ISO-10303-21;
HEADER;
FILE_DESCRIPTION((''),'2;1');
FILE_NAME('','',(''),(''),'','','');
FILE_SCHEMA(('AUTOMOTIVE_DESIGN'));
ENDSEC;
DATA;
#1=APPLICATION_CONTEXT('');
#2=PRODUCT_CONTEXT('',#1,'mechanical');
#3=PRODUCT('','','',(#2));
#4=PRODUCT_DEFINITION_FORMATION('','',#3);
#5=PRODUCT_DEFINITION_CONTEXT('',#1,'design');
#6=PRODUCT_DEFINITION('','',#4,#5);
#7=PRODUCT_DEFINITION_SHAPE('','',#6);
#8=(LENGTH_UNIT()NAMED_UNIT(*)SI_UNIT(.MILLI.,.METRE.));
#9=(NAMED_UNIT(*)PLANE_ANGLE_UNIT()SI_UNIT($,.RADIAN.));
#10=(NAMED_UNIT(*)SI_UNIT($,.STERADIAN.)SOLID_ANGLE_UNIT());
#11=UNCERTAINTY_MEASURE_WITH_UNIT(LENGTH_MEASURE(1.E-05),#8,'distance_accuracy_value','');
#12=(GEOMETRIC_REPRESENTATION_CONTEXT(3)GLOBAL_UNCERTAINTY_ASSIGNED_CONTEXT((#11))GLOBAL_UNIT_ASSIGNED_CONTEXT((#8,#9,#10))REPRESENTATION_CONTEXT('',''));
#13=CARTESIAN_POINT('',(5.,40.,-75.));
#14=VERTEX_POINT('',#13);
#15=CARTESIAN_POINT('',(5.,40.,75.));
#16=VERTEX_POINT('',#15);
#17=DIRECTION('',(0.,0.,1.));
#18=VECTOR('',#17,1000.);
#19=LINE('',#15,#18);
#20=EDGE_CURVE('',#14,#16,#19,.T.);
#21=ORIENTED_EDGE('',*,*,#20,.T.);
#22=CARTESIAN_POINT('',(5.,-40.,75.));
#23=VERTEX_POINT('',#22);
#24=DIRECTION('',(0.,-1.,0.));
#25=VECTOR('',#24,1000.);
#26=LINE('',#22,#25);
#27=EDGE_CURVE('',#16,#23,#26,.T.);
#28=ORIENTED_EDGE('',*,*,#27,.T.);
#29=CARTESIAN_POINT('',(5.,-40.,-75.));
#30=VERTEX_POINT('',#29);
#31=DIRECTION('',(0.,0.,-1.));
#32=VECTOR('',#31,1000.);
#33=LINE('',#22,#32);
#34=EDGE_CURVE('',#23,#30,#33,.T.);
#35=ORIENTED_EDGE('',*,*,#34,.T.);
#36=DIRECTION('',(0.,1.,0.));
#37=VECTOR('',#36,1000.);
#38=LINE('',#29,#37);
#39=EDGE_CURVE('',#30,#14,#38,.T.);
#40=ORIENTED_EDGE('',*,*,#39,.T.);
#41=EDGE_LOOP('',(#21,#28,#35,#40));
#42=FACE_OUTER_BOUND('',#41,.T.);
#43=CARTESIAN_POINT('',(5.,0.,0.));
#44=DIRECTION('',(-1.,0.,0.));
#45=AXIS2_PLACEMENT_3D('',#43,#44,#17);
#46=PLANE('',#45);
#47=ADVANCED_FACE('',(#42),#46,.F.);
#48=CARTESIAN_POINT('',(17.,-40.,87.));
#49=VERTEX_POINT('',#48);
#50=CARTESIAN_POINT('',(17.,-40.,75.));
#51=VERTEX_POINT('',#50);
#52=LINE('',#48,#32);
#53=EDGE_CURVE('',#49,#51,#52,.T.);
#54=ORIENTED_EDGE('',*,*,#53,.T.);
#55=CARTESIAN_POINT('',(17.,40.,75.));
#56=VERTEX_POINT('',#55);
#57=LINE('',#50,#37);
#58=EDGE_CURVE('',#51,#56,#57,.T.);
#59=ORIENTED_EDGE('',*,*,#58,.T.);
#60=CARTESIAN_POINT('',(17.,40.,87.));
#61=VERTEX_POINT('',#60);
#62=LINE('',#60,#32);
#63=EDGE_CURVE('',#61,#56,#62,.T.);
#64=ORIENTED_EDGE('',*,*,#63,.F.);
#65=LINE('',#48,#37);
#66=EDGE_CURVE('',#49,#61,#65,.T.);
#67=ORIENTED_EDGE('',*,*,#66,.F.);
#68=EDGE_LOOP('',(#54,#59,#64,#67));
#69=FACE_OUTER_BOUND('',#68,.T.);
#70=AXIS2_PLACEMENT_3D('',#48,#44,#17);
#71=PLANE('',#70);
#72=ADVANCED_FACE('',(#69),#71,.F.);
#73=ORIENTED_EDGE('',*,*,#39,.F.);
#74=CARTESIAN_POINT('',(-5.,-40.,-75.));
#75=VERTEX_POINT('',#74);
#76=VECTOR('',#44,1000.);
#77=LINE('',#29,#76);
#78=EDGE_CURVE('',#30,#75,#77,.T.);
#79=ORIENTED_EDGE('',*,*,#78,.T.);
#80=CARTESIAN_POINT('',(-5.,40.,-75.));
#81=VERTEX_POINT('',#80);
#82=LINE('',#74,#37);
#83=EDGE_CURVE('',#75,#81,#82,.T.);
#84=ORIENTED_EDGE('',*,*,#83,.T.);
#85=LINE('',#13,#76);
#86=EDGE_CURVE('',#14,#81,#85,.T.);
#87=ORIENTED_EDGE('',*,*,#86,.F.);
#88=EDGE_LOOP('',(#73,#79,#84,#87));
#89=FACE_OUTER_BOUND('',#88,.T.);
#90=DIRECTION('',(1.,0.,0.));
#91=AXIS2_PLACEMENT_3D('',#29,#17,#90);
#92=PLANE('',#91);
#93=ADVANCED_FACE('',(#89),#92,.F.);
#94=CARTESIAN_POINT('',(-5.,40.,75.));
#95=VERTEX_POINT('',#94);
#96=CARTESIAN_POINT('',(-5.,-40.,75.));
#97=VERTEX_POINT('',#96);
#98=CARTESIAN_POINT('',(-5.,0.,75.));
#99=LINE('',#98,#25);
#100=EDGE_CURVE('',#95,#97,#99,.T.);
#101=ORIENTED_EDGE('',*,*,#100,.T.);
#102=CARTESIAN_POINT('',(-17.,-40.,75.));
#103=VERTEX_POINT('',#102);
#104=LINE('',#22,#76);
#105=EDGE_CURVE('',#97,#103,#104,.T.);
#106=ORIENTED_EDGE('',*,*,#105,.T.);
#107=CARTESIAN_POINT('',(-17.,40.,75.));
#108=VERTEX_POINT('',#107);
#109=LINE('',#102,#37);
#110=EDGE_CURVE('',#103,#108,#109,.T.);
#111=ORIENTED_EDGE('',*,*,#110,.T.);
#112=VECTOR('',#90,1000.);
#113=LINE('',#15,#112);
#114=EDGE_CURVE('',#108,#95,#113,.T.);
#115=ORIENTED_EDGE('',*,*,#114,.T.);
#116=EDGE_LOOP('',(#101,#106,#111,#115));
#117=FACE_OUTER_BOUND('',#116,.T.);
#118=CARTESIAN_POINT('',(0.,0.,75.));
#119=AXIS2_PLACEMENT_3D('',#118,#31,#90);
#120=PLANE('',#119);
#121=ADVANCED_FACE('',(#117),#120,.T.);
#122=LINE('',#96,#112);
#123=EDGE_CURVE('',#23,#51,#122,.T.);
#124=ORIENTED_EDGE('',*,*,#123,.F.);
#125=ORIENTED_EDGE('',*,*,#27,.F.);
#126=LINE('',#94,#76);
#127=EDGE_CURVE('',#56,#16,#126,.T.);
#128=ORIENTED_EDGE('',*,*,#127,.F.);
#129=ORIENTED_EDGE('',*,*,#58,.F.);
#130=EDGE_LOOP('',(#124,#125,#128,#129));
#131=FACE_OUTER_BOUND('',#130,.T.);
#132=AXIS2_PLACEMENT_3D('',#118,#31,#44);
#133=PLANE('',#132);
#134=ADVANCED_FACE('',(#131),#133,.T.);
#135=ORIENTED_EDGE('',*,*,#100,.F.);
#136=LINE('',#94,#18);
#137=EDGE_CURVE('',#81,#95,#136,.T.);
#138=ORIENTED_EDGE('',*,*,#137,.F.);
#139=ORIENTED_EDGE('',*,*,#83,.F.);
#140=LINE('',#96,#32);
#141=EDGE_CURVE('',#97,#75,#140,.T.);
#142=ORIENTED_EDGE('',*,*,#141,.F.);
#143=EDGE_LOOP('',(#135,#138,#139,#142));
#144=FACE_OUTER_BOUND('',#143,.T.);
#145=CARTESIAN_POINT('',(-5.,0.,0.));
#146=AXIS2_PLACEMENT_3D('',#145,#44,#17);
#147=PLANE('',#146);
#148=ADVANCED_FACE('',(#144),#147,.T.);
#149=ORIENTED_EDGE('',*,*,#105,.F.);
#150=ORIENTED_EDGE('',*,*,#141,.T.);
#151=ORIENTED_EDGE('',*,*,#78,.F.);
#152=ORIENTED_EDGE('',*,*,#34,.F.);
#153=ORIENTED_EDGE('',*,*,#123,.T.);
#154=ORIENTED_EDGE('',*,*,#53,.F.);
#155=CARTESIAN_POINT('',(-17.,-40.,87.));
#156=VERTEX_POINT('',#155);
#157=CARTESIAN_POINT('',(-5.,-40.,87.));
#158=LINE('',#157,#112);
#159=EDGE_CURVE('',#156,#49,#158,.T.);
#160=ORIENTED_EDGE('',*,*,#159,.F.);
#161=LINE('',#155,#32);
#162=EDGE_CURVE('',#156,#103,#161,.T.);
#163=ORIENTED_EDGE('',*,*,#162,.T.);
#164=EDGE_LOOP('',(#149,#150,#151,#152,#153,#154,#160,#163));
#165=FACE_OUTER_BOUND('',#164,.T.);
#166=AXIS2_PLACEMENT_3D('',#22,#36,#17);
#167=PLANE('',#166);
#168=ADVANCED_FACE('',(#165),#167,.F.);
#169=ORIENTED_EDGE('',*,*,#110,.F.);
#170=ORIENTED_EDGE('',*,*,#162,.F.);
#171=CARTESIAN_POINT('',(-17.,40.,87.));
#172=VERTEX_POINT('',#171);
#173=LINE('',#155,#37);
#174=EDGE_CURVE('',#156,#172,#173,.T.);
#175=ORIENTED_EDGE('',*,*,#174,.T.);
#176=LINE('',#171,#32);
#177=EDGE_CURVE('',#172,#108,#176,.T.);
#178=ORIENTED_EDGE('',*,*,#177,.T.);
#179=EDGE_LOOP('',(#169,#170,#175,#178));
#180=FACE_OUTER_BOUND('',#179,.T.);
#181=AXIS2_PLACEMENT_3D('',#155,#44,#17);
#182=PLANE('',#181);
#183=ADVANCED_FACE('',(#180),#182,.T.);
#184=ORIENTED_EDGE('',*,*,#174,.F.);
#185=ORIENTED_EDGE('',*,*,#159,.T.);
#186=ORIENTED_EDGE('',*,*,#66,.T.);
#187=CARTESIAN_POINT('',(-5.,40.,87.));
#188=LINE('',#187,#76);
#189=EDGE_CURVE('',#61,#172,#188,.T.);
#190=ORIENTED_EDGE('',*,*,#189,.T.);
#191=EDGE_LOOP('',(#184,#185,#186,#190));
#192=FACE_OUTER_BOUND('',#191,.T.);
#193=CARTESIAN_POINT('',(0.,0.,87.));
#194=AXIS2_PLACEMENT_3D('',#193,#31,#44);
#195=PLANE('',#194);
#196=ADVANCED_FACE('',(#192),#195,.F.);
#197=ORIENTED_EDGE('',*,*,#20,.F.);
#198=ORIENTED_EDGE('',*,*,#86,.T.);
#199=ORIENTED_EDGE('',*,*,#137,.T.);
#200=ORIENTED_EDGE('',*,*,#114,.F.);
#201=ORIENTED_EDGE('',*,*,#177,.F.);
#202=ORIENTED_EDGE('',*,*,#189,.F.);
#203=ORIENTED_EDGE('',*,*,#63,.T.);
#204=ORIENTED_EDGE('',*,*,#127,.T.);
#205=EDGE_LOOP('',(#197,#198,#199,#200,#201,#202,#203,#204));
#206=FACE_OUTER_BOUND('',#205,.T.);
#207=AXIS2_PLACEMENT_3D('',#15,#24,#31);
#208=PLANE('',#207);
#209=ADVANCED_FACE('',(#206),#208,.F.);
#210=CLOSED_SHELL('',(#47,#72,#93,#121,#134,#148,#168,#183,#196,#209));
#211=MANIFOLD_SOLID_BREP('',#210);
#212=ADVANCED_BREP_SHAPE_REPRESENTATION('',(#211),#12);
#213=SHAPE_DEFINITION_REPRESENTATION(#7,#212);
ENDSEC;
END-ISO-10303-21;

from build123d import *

# Parameters (mm, degrees)
SKETCH_1_W      = 150
SKETCH_1_H      = 80
EXTRUDE_1_DEPTH = 5
SKETCH_2_W      = 22
SKETCH_2_H      = 80
EXTRUDE_2_DEPTH = 12


with BuildPart() as part:
    # 草图1 → 凸台-拉伸1 (new, symmetric)
    with BuildSketch(Plane(origin=(0, 0, 0), x_dir=(0, 0, -1), z_dir=(1, 0, 0))):
        Rectangle(SKETCH_1_W, SKETCH_1_H)
    extrude(amount=EXTRUDE_1_DEPTH, both=True)

    # 草图2 → 凸台-拉伸2 (add)
    with BuildSketch(Plane.XY.offset(75)):
        with Locations((6, 0)):
            Rectangle(SKETCH_2_W, SKETCH_2_H)
    extrude_2 = extrude(amount=EXTRUDE_2_DEPTH)

    # 镜向1: 凸台-拉伸2 across plane
    add(extrude_2.mirror(Plane(origin=(0, 0, 0), x_dir=(0, 0, 1), z_dir=(1, 0, 0))))


solid = part.part
